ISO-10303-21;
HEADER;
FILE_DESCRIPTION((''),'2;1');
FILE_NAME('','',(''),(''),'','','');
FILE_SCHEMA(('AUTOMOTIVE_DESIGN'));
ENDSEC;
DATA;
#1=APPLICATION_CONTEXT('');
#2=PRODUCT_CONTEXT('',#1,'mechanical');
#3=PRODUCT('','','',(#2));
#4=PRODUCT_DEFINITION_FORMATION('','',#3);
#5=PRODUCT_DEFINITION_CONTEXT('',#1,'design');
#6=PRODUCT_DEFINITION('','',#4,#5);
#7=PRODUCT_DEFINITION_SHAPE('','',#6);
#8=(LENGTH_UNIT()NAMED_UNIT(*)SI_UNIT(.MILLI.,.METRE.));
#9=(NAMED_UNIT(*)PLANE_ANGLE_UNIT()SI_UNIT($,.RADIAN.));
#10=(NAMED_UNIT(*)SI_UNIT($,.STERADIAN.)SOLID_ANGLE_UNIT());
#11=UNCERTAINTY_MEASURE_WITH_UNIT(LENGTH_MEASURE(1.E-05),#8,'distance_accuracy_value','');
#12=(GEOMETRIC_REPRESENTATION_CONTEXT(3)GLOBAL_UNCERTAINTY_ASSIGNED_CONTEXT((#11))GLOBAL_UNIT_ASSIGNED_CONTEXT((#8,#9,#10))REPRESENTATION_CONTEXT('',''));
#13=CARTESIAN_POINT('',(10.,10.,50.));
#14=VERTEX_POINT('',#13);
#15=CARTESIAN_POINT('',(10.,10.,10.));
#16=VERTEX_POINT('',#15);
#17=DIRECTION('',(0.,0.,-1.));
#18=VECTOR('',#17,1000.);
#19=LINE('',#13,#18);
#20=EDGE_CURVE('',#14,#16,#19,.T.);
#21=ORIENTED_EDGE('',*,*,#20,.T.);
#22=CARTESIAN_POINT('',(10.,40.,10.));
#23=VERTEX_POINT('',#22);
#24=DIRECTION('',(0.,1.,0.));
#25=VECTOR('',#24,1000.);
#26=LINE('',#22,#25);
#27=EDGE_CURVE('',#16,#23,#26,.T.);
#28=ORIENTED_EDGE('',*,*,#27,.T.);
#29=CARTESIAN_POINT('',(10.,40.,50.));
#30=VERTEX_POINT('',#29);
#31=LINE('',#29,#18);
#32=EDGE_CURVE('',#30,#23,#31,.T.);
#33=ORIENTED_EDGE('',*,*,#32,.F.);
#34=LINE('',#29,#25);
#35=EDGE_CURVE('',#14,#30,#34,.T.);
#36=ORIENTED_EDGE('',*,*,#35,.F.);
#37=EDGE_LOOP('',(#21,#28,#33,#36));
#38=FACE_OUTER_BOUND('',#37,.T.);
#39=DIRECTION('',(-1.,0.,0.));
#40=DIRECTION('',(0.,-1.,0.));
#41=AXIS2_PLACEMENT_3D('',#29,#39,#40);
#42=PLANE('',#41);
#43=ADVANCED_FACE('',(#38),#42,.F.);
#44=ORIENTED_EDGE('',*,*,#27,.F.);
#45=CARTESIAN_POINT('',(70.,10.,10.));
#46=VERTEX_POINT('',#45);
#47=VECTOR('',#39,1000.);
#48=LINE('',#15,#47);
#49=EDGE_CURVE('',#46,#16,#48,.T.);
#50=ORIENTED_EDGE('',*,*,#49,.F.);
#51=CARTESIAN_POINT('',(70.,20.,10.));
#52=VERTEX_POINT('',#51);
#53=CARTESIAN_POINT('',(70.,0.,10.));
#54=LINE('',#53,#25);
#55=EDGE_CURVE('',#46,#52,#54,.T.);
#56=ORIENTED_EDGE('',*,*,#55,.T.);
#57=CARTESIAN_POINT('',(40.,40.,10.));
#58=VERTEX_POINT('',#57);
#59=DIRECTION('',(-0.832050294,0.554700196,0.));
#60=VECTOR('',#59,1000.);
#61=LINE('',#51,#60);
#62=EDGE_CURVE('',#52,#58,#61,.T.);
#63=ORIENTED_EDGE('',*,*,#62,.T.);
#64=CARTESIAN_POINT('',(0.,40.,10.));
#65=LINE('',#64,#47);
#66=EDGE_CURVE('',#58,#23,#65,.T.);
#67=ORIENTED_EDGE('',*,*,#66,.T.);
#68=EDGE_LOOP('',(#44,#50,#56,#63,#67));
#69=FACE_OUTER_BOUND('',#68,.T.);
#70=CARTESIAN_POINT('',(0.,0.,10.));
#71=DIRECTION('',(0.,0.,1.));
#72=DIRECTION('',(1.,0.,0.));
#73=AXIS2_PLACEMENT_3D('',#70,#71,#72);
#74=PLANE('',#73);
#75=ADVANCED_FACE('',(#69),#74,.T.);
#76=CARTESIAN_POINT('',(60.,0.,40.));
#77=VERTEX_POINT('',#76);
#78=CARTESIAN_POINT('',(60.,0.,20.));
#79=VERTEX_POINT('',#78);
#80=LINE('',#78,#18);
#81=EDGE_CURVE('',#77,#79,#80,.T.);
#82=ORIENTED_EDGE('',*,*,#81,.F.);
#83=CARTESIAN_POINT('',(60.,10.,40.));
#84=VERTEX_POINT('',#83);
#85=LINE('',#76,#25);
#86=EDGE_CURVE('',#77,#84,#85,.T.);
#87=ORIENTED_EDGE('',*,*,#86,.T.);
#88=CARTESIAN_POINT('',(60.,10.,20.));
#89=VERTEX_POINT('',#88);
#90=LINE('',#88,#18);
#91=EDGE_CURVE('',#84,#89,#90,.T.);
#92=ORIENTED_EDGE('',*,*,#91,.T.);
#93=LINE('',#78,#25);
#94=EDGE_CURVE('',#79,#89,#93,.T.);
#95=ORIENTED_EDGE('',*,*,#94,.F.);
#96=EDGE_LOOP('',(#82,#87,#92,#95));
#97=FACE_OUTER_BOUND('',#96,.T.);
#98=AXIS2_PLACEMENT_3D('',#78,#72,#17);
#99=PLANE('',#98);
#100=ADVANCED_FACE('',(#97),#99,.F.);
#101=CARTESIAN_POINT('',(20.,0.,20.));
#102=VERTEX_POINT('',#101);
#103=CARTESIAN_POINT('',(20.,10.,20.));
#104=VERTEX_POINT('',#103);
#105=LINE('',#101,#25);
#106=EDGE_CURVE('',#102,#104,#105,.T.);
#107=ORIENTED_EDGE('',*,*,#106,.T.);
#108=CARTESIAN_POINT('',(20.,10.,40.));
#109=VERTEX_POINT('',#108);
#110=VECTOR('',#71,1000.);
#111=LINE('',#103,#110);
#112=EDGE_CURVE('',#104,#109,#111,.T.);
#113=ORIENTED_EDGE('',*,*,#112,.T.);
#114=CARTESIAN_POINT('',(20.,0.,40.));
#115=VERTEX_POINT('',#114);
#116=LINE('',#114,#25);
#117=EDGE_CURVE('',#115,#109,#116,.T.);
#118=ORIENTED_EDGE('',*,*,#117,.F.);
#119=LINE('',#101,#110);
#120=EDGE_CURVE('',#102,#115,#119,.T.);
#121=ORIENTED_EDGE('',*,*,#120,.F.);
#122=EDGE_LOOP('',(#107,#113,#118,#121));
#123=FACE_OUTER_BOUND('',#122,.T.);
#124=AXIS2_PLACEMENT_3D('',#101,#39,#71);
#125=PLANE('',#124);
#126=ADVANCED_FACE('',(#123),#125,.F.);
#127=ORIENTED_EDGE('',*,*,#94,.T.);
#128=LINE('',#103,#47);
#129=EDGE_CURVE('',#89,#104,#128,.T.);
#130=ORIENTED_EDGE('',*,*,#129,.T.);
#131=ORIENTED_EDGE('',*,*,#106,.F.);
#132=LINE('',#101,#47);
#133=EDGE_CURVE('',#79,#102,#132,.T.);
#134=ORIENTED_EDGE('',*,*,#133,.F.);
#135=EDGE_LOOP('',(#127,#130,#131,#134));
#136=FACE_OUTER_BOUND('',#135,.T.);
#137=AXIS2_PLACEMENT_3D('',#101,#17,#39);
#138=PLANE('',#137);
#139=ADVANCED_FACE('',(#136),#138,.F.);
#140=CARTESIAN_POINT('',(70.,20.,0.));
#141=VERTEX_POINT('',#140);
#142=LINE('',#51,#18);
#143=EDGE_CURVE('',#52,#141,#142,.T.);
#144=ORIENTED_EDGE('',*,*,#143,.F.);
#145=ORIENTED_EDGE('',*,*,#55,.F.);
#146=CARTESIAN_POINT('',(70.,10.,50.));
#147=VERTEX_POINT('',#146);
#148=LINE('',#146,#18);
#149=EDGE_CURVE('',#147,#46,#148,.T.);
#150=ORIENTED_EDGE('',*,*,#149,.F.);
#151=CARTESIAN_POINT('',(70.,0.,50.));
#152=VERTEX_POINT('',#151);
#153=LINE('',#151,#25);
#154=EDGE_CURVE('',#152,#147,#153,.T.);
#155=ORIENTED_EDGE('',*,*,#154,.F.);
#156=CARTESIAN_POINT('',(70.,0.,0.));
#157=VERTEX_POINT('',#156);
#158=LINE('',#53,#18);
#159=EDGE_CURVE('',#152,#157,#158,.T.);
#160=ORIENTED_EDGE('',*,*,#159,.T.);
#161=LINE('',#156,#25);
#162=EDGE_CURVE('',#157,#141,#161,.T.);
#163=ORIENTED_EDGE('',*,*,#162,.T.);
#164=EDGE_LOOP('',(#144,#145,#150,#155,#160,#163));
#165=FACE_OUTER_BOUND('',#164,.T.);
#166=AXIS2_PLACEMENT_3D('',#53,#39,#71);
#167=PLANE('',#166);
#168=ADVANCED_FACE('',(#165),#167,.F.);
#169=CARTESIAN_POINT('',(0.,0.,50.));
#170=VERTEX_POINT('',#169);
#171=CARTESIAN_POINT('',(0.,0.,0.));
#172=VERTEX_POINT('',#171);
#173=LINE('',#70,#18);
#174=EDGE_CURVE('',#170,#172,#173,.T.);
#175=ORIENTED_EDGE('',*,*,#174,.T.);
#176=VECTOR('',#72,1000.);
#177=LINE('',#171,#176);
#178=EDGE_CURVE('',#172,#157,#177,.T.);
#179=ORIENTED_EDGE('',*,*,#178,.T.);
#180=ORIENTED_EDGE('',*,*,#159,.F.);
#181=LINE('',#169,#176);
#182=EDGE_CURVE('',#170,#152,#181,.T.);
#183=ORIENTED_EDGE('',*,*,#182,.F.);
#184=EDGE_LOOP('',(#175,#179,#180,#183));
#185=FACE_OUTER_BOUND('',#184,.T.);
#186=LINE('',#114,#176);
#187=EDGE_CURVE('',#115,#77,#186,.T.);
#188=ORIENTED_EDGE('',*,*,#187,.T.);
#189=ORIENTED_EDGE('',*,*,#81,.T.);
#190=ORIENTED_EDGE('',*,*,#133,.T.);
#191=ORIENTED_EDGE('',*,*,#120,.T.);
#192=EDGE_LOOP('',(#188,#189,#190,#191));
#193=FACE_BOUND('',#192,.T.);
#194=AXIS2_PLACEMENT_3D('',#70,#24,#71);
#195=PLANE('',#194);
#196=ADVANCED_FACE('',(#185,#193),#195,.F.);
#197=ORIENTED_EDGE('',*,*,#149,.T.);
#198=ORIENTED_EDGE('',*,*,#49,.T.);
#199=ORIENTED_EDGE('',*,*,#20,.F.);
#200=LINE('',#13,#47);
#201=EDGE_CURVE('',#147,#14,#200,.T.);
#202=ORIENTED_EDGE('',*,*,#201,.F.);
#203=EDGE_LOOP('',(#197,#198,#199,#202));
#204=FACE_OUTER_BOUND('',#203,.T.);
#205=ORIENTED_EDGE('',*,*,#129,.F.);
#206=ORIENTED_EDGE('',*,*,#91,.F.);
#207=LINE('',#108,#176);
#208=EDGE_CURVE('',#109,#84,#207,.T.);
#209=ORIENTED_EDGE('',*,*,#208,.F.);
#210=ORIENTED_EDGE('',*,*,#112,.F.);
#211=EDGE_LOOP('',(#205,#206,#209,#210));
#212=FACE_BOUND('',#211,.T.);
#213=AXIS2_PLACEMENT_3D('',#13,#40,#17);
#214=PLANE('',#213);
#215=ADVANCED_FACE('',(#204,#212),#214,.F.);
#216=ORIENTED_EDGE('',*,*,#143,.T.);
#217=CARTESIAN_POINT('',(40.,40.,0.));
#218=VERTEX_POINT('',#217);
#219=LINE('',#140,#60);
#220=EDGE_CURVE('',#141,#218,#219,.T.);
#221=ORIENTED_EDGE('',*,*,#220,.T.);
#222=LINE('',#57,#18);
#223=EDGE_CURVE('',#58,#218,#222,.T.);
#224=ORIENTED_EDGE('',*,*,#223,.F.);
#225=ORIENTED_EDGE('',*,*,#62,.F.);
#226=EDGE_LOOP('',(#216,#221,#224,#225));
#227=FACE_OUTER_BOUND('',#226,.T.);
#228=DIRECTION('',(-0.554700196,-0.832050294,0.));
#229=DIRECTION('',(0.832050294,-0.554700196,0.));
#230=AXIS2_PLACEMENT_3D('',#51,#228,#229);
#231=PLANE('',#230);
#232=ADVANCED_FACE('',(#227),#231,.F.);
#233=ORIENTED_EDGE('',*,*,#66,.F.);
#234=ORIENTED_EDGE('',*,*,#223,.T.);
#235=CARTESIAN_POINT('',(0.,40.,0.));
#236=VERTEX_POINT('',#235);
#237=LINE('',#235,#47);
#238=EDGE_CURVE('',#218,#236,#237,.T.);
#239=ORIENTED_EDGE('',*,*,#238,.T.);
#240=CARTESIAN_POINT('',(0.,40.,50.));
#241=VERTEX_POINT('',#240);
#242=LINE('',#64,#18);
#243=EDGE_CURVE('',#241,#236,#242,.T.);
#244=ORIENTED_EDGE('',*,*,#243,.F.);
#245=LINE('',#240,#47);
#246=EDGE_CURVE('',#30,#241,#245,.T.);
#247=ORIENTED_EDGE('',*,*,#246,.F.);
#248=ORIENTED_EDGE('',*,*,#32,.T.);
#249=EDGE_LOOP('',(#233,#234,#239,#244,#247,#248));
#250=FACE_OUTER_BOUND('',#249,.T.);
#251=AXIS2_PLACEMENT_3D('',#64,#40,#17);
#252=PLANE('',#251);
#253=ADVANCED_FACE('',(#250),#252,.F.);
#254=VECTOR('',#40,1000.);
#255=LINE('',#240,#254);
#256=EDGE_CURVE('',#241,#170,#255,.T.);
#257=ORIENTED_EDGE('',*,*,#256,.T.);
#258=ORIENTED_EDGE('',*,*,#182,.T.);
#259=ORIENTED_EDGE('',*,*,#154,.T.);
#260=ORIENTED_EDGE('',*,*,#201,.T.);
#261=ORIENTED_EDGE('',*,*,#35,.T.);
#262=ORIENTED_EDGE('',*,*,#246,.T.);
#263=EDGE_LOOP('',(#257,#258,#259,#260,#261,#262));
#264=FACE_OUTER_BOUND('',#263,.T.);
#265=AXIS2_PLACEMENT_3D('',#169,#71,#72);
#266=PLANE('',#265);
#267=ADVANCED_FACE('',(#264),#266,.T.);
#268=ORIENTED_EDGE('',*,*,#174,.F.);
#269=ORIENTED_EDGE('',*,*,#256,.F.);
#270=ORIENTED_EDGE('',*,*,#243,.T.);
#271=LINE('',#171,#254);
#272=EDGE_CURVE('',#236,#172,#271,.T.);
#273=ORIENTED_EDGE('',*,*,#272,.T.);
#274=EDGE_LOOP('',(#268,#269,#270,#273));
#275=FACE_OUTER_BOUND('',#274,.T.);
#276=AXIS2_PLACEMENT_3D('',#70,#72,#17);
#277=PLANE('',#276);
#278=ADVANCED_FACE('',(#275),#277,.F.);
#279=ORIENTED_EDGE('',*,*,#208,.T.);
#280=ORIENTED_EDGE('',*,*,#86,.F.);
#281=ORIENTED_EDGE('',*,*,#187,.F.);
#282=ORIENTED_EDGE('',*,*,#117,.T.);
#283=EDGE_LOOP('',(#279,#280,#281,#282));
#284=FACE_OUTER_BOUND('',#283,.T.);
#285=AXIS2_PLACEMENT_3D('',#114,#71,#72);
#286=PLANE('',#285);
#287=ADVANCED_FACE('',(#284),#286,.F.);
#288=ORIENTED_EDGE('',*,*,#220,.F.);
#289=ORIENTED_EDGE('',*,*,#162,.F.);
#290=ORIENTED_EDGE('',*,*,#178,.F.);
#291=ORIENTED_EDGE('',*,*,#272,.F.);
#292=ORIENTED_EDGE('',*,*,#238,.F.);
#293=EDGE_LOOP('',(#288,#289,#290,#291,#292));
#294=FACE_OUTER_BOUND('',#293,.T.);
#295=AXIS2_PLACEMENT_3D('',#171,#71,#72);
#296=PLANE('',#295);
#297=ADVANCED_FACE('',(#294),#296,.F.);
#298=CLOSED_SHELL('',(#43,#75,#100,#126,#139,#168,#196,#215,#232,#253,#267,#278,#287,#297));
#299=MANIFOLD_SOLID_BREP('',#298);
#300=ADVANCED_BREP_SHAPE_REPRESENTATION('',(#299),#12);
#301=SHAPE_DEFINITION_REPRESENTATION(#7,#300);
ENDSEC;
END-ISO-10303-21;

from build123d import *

# Parameters (mm, degrees)
CHAMFERED_END_WALL_DEPTH = 10
BACK_WALL_SKETCH_W       = 10
BACK_WALL_SKETCH_H       = 40
BACK_WALL_DEPTH          = 40
BASE_PLATE_SKETCH_W      = 60
BASE_PLATE_SKETCH_H      = 10
BASE_PLATE_DEPTH         = 40
BASE_SLOT_SKETCH_W       = 40
BASE_SLOT_SKETCH_H       = 20
BASE_SLOT_40X20_DEPTH    = 10


with BuildPart() as part:
    # End Wall Profile Sketch → Chamfered End Wall (new body)
    with BuildSketch(Plane.XY):
        Polygon((0, 0), (0, 40), (40, 40), (70, 20), (70, 0), align=None)
    extrude(amount=CHAMFERED_END_WALL_DEPTH)

    # Back Wall Sketch → Back Wall (add)
    with BuildSketch(Plane.XY.offset(10)):
        with Locations((5, 20)):
            Rectangle(BACK_WALL_SKETCH_W, BACK_WALL_SKETCH_H)
    extrude(amount=BACK_WALL_DEPTH)

    # Base Plate Sketch → Base Plate (add)
    with BuildSketch(Plane.XY.offset(10)):
        with Locations((40, 5)):
            Rectangle(BASE_PLATE_SKETCH_W, BASE_PLATE_SKETCH_H)
    extrude(amount=BASE_PLATE_DEPTH)

    # Base Slot Sketch → Base Slot 40x20 (cut)
    with BuildSketch(Plane(origin=(0, 10, 0), x_dir=(1, 0, 0), z_dir=(0, 1, 0))):
        with Locations((40, -30)):
            Rectangle(BASE_SLOT_SKETCH_W, BASE_SLOT_SKETCH_H)
    extrude(amount=-BASE_SLOT_40X20_DEPTH, mode=Mode.SUBTRACT)


solid = part.part
